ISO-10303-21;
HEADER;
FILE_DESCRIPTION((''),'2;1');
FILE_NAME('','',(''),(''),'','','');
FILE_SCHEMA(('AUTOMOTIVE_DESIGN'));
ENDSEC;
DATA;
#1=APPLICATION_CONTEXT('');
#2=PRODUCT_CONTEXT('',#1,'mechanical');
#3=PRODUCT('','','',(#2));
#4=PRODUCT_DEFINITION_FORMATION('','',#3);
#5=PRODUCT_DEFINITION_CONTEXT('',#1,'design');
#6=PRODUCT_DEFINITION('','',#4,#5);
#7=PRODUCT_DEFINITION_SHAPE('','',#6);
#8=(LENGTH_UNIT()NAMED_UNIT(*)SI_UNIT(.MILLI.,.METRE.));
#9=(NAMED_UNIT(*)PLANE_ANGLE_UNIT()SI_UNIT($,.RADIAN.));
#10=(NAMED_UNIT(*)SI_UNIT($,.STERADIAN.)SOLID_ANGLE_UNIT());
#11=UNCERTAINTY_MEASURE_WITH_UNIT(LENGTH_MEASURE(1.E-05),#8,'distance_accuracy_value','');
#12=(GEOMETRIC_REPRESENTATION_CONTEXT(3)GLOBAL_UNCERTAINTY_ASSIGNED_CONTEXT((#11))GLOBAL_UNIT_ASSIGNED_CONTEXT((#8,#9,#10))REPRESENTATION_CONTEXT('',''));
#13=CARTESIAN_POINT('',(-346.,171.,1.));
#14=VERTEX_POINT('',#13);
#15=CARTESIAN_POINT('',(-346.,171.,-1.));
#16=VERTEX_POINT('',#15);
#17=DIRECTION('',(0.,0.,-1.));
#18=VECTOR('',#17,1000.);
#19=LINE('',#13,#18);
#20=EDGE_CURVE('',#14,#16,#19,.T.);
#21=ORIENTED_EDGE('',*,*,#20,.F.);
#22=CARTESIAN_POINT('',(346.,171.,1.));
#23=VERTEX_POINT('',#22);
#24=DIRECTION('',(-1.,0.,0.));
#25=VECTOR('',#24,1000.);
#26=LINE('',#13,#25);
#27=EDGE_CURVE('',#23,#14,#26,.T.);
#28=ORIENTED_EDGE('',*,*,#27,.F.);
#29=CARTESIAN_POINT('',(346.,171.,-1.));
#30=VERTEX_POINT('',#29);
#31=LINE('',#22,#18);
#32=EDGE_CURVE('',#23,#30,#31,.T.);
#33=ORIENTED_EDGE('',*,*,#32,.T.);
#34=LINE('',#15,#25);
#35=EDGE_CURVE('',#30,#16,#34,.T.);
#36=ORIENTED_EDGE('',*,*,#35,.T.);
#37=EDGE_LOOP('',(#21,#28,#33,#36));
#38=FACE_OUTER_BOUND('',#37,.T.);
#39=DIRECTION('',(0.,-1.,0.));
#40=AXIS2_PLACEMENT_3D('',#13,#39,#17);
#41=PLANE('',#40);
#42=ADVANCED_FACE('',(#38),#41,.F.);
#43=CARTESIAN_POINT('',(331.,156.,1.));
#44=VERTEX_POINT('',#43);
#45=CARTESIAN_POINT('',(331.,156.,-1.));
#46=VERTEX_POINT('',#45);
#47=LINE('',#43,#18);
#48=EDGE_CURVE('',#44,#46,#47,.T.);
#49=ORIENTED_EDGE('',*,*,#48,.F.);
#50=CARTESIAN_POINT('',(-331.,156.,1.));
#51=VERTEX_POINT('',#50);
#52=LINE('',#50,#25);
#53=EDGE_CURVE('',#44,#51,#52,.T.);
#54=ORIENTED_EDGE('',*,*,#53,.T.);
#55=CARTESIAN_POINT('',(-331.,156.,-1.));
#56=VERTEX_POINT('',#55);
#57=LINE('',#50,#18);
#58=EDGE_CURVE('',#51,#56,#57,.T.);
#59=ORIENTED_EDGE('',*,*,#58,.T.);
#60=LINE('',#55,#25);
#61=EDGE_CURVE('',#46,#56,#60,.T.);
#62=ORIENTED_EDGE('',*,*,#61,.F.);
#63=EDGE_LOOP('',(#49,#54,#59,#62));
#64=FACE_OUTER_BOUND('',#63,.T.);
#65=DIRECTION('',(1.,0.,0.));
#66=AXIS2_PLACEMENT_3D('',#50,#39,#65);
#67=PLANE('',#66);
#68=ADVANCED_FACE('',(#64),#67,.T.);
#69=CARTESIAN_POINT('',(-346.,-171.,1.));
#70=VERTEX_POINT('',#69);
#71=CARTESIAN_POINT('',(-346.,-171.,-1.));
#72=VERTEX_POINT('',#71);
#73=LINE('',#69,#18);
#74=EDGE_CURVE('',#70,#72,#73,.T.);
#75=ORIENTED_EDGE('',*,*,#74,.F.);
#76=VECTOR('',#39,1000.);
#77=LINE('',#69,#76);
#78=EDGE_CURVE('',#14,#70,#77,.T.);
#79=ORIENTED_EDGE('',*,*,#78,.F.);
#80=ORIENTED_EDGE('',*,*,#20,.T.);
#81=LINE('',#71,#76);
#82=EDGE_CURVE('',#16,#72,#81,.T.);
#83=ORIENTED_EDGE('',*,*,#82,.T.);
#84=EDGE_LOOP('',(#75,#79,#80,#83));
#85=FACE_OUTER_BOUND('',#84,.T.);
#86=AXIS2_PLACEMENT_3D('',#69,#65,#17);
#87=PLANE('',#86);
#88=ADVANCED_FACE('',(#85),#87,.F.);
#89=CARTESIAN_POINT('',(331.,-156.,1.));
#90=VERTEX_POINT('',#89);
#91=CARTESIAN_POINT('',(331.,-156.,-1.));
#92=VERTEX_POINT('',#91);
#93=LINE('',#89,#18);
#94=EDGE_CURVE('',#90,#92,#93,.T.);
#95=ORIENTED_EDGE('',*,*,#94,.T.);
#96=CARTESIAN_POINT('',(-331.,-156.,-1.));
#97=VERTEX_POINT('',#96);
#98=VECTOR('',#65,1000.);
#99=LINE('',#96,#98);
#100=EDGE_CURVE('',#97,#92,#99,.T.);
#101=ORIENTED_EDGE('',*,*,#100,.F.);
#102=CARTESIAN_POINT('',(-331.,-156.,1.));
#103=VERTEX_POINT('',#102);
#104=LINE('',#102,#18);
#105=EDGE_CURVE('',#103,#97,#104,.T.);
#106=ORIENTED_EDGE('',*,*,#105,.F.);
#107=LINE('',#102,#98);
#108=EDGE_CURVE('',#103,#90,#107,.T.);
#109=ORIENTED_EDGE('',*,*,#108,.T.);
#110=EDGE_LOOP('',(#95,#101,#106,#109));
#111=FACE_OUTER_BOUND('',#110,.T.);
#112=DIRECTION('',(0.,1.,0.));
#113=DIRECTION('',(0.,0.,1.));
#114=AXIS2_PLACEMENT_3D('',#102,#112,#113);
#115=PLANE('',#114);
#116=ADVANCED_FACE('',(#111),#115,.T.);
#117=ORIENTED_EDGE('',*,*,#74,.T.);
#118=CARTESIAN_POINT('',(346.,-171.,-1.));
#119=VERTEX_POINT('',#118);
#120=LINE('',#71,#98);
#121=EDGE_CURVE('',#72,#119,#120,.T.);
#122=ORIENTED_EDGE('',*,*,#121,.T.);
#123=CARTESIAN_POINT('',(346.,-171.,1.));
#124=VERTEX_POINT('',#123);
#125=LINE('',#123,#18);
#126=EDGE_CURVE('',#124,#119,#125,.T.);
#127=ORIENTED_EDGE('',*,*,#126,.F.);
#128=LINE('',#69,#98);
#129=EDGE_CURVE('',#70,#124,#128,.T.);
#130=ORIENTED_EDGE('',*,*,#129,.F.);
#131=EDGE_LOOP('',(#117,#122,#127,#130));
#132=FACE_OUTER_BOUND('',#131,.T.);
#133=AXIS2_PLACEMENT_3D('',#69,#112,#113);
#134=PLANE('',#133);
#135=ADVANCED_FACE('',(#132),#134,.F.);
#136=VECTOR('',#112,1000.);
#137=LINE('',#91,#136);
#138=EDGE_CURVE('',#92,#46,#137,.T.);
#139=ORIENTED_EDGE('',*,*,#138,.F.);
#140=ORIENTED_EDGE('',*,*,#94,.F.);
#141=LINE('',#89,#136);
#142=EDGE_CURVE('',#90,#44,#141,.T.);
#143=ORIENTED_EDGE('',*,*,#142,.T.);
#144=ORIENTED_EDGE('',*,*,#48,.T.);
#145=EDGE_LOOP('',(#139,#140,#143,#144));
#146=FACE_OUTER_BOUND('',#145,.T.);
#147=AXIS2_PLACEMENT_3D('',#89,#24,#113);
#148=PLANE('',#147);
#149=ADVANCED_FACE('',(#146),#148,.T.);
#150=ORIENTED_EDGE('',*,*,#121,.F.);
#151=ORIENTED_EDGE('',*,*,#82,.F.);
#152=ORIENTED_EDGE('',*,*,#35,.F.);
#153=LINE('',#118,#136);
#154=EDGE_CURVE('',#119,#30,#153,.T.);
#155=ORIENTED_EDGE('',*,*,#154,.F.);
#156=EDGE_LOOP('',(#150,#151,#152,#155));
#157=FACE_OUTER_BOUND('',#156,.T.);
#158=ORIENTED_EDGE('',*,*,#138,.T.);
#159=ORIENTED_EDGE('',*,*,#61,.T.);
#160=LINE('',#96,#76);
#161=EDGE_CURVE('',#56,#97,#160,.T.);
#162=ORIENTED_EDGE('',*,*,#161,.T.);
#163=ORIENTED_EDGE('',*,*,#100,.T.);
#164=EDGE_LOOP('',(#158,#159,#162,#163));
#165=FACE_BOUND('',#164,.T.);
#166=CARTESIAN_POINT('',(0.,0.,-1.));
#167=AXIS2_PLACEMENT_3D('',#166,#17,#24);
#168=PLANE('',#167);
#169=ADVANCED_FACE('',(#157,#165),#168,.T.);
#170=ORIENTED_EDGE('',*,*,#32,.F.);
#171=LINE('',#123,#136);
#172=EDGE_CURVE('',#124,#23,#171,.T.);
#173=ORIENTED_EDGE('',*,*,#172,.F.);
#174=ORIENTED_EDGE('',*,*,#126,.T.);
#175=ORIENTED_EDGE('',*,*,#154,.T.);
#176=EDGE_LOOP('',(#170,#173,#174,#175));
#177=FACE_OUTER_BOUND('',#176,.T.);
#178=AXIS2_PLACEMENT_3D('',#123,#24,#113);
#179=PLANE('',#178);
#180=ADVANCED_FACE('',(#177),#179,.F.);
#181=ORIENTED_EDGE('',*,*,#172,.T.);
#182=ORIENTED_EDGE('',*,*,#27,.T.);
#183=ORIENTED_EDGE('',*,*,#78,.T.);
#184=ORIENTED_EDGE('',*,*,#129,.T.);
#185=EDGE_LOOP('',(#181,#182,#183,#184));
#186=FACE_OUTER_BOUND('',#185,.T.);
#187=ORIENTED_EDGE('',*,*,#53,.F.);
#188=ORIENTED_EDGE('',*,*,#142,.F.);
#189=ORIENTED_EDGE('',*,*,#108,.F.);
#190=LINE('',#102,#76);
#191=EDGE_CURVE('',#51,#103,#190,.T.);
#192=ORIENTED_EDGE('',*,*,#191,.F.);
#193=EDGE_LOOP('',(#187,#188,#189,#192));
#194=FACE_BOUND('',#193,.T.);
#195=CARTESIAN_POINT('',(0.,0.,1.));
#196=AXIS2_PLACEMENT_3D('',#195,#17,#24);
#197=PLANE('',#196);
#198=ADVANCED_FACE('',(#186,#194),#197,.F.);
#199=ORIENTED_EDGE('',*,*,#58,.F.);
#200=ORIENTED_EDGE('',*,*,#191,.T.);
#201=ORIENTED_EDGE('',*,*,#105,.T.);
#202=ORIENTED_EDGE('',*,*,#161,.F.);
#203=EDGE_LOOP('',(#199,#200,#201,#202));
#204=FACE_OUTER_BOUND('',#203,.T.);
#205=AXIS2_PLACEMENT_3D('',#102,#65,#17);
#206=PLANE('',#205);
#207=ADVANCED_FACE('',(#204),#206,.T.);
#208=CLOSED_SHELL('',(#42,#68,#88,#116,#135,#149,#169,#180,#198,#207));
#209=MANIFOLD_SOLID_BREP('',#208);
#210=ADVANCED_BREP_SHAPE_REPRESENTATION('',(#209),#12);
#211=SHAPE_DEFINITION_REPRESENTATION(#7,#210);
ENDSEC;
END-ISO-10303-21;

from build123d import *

# Parameters (mm, degrees)
SKETCH_1_W      = 692
SKETCH_1_H      = 342
SKETCH_1_W_2    = 662
SKETCH_1_H_2    = 312
EXTRUDE_1_DEPTH = 1


with BuildPart() as part:
    # 草图1 → 凸台-拉伸1 (new, symmetric)
    with BuildSketch(Plane.XY):
        Rectangle(SKETCH_1_W, SKETCH_1_H)
        Rectangle(SKETCH_1_W_2, SKETCH_1_H_2, mode=Mode.SUBTRACT)
    extrude(amount=EXTRUDE_1_DEPTH, both=True)


solid = part.part
